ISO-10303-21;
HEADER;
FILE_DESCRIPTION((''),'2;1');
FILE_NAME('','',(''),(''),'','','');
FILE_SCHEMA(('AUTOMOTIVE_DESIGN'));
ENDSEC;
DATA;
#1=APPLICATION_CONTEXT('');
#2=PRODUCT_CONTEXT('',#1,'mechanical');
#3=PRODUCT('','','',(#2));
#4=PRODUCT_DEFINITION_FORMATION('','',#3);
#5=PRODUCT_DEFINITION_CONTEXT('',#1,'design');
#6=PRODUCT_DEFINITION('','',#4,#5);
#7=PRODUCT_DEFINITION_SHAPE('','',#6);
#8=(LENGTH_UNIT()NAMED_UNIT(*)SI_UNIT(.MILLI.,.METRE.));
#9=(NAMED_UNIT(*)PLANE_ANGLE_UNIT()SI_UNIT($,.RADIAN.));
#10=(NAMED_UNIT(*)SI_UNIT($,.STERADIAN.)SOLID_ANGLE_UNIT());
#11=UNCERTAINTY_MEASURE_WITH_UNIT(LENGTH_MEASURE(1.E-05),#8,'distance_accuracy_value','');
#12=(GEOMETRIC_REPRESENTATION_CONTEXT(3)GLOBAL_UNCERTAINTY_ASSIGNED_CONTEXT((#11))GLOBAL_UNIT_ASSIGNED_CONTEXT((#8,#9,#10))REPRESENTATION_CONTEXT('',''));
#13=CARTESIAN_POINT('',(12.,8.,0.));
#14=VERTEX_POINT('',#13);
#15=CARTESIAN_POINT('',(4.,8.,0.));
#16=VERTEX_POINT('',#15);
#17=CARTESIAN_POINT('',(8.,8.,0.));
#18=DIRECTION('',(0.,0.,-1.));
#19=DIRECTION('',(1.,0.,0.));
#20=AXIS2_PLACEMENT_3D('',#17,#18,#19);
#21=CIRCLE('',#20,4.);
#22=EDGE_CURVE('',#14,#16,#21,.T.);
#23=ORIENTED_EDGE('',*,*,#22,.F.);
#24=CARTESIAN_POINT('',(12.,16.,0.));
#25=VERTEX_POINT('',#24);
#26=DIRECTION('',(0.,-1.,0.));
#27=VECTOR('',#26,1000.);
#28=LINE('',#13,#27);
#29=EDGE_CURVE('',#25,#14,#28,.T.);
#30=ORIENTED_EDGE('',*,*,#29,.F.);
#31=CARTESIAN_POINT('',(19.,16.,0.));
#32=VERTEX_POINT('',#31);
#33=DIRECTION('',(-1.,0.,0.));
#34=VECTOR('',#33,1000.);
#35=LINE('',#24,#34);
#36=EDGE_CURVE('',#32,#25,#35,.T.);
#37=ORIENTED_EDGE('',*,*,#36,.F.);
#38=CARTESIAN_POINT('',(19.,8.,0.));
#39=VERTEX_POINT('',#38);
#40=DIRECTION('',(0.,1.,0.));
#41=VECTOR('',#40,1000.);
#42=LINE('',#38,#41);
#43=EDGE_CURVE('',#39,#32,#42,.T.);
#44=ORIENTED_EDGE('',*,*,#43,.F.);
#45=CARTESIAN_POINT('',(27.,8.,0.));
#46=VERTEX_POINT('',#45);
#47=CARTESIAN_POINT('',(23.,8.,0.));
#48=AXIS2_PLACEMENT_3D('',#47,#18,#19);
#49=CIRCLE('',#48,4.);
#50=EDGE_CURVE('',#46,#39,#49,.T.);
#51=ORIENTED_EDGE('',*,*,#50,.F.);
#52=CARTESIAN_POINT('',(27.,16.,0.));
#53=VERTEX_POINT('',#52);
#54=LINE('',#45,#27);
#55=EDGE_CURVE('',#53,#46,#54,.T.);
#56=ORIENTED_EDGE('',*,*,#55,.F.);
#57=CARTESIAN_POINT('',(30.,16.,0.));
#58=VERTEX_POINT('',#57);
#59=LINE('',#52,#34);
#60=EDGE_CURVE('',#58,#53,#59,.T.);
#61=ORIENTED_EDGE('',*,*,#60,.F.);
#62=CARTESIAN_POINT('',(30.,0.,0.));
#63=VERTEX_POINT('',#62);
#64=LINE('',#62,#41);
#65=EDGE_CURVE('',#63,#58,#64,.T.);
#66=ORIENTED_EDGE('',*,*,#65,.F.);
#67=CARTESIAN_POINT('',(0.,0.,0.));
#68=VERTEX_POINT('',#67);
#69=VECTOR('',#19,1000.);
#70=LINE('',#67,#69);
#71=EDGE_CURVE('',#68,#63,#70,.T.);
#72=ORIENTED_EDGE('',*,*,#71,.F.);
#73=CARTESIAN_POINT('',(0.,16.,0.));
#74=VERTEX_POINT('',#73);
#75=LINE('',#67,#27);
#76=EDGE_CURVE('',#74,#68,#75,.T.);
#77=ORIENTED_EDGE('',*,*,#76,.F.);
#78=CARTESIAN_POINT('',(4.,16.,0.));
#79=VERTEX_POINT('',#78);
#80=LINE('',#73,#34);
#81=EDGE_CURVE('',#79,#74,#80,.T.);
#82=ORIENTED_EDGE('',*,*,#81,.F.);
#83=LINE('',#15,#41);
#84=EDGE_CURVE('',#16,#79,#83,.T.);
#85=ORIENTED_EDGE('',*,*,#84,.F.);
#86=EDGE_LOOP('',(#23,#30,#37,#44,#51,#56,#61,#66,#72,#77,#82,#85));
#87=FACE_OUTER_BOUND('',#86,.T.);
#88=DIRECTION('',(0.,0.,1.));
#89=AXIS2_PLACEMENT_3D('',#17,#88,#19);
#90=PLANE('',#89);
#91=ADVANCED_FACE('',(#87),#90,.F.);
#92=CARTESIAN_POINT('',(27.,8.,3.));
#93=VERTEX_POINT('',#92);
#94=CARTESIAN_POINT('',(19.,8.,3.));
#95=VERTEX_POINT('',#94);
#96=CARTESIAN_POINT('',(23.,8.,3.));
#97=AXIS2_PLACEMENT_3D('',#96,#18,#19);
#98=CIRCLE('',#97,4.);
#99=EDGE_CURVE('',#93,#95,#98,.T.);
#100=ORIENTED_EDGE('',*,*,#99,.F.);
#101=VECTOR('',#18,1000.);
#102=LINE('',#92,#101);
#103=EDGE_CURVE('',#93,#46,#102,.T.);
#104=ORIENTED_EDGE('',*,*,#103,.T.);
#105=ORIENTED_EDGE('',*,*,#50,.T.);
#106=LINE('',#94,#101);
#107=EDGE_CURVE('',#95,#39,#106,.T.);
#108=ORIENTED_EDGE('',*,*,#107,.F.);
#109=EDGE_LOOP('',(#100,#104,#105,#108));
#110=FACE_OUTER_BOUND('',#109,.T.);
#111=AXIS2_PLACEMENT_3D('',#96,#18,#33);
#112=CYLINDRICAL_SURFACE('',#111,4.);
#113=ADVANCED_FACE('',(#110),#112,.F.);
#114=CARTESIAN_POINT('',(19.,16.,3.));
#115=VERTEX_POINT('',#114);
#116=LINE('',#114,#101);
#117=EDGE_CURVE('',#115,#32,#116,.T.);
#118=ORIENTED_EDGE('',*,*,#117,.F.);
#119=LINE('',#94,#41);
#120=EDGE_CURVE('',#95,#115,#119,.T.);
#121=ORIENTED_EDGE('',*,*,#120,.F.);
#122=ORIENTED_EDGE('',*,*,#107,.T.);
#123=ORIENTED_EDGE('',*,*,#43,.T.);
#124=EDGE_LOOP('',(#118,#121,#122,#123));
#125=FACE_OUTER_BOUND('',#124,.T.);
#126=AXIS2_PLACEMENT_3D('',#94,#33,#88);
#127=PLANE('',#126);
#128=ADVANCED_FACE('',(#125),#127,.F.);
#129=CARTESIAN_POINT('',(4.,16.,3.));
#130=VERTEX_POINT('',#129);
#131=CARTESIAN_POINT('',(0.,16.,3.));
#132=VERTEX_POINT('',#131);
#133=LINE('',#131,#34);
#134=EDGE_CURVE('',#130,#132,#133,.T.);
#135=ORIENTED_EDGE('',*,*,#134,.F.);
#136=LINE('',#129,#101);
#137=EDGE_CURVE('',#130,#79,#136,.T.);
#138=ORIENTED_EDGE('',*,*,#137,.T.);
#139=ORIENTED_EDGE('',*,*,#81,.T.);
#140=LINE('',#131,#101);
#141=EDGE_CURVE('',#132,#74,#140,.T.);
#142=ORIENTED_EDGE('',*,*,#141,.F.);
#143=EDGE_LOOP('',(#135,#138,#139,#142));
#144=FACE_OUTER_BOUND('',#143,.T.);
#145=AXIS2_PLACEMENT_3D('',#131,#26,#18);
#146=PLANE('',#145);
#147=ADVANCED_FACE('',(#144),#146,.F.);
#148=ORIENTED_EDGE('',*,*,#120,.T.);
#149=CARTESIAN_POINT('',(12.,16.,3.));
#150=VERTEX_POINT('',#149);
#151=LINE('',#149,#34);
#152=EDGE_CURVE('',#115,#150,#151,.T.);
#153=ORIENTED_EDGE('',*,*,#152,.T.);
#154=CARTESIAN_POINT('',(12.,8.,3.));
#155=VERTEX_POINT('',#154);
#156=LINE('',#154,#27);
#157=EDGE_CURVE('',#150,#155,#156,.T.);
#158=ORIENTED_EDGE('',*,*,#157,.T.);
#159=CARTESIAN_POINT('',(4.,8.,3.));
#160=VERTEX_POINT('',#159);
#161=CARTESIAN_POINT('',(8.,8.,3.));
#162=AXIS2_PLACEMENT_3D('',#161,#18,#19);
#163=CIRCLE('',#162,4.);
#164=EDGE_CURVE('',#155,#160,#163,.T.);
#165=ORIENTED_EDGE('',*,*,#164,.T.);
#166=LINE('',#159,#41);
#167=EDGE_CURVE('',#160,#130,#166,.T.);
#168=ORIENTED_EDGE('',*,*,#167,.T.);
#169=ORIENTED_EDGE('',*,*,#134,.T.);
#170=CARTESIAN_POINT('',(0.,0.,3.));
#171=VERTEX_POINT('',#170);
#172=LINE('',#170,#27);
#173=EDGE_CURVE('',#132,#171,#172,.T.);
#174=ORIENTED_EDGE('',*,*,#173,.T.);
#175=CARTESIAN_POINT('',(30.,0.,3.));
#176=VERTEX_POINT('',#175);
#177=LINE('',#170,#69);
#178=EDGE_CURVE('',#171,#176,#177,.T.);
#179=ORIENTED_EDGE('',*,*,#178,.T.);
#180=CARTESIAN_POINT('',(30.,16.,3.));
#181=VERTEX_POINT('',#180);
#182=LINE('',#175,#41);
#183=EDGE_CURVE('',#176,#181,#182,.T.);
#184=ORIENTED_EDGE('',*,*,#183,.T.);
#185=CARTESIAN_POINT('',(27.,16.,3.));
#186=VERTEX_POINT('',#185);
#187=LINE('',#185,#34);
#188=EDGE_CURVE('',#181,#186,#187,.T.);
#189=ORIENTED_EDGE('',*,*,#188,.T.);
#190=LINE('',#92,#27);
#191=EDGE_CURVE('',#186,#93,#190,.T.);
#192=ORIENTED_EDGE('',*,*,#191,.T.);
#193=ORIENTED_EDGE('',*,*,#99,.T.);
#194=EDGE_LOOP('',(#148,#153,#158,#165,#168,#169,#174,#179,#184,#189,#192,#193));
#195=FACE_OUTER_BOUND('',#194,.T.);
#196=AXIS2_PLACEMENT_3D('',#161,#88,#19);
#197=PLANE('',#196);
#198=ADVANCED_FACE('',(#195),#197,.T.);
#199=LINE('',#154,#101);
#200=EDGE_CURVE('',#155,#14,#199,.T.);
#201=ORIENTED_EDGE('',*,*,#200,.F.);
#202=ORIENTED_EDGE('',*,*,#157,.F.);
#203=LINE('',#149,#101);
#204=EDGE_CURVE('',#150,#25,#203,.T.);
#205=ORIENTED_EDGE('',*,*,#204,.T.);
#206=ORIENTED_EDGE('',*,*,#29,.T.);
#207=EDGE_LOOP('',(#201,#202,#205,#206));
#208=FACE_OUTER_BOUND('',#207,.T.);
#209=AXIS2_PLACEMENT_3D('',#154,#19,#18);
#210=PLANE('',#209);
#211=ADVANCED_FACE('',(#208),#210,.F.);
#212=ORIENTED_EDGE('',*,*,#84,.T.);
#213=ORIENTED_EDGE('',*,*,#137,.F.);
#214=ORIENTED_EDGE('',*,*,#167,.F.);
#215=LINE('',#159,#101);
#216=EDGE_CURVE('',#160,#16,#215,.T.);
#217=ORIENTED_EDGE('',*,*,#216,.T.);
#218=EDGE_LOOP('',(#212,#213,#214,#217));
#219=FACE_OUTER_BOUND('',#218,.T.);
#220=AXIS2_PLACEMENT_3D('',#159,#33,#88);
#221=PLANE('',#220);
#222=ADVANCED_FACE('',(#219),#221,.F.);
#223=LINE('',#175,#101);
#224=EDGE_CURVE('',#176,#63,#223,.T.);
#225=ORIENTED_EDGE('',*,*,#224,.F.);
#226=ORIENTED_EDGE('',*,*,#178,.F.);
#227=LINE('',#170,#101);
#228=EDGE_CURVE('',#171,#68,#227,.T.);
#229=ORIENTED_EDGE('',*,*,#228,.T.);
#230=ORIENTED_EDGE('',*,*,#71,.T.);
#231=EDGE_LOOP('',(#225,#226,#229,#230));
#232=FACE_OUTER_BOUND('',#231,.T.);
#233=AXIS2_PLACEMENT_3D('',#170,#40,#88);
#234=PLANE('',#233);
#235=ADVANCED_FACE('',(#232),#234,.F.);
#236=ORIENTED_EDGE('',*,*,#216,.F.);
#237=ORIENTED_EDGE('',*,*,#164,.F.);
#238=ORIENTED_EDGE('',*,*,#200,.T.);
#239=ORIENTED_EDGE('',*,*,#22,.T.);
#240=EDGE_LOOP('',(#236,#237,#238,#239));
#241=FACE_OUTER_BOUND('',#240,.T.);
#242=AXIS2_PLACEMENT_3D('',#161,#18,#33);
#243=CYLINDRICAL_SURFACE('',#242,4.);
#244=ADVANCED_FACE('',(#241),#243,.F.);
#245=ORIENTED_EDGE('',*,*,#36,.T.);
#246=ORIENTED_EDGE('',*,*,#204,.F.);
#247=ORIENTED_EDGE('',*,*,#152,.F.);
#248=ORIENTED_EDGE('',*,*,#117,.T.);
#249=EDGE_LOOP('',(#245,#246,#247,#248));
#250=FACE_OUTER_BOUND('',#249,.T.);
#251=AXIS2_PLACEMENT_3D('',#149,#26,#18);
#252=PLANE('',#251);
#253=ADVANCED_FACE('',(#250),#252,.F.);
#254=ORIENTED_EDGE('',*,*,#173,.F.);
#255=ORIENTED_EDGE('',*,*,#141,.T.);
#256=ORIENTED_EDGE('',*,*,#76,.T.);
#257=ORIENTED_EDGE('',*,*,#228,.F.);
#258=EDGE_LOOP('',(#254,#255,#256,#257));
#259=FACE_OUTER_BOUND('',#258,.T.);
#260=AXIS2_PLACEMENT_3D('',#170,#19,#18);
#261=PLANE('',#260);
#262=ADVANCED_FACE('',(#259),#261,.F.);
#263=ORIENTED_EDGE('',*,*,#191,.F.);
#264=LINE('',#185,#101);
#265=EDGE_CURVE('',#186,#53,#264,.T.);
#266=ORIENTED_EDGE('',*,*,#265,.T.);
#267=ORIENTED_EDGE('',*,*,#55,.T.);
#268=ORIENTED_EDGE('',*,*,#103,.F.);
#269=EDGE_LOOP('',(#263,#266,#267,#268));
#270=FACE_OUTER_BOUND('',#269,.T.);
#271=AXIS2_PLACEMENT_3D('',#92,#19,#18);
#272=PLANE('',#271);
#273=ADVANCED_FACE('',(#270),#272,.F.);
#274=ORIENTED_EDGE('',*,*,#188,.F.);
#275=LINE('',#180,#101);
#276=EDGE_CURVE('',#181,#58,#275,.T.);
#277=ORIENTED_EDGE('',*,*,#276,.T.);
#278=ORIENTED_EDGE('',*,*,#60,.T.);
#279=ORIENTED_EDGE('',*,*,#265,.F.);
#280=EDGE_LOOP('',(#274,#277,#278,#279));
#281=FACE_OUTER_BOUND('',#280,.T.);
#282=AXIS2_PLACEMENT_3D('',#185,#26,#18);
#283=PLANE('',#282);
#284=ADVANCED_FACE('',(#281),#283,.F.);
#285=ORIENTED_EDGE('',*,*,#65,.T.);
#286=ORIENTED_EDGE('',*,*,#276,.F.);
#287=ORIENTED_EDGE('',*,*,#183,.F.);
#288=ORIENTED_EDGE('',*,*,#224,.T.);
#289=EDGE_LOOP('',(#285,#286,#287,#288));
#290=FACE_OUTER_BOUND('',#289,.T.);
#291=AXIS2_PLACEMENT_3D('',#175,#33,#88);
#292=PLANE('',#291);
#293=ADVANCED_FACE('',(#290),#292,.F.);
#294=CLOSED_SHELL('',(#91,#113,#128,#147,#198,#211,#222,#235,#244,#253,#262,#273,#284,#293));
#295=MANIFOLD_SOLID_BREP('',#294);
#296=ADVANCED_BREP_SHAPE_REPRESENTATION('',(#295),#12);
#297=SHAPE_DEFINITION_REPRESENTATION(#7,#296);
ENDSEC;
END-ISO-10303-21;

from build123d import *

# Parameters (mm, degrees)
BOSS_EXTRUDE1_DEPTH = 3


with BuildPart() as part:
    # Sketch1 → Boss-Extrude1 (new body)
    with BuildSketch(Plane.XY):
        with BuildLine():
            Line((0, 0), (30, 0))
            Line((30, 0), (30, 16))
            Line((30, 16), (27, 16))
            Line((27, 16), (27, 8))
            ThreePointArc((27, 8), (23, 4), (19, 8))
            Line((19, 8), (19, 16))
            Line((19, 16), (12, 16))
            Line((12, 16), (12, 8))
            ThreePointArc((12, 8), (8, 4), (4, 8))
            Line((4, 8), (4, 16))
            Line((4, 16), (0, 16))
            Line((0, 16), (0, 0))
        make_face()
    extrude(amount=BOSS_EXTRUDE1_DEPTH)


solid = part.part
